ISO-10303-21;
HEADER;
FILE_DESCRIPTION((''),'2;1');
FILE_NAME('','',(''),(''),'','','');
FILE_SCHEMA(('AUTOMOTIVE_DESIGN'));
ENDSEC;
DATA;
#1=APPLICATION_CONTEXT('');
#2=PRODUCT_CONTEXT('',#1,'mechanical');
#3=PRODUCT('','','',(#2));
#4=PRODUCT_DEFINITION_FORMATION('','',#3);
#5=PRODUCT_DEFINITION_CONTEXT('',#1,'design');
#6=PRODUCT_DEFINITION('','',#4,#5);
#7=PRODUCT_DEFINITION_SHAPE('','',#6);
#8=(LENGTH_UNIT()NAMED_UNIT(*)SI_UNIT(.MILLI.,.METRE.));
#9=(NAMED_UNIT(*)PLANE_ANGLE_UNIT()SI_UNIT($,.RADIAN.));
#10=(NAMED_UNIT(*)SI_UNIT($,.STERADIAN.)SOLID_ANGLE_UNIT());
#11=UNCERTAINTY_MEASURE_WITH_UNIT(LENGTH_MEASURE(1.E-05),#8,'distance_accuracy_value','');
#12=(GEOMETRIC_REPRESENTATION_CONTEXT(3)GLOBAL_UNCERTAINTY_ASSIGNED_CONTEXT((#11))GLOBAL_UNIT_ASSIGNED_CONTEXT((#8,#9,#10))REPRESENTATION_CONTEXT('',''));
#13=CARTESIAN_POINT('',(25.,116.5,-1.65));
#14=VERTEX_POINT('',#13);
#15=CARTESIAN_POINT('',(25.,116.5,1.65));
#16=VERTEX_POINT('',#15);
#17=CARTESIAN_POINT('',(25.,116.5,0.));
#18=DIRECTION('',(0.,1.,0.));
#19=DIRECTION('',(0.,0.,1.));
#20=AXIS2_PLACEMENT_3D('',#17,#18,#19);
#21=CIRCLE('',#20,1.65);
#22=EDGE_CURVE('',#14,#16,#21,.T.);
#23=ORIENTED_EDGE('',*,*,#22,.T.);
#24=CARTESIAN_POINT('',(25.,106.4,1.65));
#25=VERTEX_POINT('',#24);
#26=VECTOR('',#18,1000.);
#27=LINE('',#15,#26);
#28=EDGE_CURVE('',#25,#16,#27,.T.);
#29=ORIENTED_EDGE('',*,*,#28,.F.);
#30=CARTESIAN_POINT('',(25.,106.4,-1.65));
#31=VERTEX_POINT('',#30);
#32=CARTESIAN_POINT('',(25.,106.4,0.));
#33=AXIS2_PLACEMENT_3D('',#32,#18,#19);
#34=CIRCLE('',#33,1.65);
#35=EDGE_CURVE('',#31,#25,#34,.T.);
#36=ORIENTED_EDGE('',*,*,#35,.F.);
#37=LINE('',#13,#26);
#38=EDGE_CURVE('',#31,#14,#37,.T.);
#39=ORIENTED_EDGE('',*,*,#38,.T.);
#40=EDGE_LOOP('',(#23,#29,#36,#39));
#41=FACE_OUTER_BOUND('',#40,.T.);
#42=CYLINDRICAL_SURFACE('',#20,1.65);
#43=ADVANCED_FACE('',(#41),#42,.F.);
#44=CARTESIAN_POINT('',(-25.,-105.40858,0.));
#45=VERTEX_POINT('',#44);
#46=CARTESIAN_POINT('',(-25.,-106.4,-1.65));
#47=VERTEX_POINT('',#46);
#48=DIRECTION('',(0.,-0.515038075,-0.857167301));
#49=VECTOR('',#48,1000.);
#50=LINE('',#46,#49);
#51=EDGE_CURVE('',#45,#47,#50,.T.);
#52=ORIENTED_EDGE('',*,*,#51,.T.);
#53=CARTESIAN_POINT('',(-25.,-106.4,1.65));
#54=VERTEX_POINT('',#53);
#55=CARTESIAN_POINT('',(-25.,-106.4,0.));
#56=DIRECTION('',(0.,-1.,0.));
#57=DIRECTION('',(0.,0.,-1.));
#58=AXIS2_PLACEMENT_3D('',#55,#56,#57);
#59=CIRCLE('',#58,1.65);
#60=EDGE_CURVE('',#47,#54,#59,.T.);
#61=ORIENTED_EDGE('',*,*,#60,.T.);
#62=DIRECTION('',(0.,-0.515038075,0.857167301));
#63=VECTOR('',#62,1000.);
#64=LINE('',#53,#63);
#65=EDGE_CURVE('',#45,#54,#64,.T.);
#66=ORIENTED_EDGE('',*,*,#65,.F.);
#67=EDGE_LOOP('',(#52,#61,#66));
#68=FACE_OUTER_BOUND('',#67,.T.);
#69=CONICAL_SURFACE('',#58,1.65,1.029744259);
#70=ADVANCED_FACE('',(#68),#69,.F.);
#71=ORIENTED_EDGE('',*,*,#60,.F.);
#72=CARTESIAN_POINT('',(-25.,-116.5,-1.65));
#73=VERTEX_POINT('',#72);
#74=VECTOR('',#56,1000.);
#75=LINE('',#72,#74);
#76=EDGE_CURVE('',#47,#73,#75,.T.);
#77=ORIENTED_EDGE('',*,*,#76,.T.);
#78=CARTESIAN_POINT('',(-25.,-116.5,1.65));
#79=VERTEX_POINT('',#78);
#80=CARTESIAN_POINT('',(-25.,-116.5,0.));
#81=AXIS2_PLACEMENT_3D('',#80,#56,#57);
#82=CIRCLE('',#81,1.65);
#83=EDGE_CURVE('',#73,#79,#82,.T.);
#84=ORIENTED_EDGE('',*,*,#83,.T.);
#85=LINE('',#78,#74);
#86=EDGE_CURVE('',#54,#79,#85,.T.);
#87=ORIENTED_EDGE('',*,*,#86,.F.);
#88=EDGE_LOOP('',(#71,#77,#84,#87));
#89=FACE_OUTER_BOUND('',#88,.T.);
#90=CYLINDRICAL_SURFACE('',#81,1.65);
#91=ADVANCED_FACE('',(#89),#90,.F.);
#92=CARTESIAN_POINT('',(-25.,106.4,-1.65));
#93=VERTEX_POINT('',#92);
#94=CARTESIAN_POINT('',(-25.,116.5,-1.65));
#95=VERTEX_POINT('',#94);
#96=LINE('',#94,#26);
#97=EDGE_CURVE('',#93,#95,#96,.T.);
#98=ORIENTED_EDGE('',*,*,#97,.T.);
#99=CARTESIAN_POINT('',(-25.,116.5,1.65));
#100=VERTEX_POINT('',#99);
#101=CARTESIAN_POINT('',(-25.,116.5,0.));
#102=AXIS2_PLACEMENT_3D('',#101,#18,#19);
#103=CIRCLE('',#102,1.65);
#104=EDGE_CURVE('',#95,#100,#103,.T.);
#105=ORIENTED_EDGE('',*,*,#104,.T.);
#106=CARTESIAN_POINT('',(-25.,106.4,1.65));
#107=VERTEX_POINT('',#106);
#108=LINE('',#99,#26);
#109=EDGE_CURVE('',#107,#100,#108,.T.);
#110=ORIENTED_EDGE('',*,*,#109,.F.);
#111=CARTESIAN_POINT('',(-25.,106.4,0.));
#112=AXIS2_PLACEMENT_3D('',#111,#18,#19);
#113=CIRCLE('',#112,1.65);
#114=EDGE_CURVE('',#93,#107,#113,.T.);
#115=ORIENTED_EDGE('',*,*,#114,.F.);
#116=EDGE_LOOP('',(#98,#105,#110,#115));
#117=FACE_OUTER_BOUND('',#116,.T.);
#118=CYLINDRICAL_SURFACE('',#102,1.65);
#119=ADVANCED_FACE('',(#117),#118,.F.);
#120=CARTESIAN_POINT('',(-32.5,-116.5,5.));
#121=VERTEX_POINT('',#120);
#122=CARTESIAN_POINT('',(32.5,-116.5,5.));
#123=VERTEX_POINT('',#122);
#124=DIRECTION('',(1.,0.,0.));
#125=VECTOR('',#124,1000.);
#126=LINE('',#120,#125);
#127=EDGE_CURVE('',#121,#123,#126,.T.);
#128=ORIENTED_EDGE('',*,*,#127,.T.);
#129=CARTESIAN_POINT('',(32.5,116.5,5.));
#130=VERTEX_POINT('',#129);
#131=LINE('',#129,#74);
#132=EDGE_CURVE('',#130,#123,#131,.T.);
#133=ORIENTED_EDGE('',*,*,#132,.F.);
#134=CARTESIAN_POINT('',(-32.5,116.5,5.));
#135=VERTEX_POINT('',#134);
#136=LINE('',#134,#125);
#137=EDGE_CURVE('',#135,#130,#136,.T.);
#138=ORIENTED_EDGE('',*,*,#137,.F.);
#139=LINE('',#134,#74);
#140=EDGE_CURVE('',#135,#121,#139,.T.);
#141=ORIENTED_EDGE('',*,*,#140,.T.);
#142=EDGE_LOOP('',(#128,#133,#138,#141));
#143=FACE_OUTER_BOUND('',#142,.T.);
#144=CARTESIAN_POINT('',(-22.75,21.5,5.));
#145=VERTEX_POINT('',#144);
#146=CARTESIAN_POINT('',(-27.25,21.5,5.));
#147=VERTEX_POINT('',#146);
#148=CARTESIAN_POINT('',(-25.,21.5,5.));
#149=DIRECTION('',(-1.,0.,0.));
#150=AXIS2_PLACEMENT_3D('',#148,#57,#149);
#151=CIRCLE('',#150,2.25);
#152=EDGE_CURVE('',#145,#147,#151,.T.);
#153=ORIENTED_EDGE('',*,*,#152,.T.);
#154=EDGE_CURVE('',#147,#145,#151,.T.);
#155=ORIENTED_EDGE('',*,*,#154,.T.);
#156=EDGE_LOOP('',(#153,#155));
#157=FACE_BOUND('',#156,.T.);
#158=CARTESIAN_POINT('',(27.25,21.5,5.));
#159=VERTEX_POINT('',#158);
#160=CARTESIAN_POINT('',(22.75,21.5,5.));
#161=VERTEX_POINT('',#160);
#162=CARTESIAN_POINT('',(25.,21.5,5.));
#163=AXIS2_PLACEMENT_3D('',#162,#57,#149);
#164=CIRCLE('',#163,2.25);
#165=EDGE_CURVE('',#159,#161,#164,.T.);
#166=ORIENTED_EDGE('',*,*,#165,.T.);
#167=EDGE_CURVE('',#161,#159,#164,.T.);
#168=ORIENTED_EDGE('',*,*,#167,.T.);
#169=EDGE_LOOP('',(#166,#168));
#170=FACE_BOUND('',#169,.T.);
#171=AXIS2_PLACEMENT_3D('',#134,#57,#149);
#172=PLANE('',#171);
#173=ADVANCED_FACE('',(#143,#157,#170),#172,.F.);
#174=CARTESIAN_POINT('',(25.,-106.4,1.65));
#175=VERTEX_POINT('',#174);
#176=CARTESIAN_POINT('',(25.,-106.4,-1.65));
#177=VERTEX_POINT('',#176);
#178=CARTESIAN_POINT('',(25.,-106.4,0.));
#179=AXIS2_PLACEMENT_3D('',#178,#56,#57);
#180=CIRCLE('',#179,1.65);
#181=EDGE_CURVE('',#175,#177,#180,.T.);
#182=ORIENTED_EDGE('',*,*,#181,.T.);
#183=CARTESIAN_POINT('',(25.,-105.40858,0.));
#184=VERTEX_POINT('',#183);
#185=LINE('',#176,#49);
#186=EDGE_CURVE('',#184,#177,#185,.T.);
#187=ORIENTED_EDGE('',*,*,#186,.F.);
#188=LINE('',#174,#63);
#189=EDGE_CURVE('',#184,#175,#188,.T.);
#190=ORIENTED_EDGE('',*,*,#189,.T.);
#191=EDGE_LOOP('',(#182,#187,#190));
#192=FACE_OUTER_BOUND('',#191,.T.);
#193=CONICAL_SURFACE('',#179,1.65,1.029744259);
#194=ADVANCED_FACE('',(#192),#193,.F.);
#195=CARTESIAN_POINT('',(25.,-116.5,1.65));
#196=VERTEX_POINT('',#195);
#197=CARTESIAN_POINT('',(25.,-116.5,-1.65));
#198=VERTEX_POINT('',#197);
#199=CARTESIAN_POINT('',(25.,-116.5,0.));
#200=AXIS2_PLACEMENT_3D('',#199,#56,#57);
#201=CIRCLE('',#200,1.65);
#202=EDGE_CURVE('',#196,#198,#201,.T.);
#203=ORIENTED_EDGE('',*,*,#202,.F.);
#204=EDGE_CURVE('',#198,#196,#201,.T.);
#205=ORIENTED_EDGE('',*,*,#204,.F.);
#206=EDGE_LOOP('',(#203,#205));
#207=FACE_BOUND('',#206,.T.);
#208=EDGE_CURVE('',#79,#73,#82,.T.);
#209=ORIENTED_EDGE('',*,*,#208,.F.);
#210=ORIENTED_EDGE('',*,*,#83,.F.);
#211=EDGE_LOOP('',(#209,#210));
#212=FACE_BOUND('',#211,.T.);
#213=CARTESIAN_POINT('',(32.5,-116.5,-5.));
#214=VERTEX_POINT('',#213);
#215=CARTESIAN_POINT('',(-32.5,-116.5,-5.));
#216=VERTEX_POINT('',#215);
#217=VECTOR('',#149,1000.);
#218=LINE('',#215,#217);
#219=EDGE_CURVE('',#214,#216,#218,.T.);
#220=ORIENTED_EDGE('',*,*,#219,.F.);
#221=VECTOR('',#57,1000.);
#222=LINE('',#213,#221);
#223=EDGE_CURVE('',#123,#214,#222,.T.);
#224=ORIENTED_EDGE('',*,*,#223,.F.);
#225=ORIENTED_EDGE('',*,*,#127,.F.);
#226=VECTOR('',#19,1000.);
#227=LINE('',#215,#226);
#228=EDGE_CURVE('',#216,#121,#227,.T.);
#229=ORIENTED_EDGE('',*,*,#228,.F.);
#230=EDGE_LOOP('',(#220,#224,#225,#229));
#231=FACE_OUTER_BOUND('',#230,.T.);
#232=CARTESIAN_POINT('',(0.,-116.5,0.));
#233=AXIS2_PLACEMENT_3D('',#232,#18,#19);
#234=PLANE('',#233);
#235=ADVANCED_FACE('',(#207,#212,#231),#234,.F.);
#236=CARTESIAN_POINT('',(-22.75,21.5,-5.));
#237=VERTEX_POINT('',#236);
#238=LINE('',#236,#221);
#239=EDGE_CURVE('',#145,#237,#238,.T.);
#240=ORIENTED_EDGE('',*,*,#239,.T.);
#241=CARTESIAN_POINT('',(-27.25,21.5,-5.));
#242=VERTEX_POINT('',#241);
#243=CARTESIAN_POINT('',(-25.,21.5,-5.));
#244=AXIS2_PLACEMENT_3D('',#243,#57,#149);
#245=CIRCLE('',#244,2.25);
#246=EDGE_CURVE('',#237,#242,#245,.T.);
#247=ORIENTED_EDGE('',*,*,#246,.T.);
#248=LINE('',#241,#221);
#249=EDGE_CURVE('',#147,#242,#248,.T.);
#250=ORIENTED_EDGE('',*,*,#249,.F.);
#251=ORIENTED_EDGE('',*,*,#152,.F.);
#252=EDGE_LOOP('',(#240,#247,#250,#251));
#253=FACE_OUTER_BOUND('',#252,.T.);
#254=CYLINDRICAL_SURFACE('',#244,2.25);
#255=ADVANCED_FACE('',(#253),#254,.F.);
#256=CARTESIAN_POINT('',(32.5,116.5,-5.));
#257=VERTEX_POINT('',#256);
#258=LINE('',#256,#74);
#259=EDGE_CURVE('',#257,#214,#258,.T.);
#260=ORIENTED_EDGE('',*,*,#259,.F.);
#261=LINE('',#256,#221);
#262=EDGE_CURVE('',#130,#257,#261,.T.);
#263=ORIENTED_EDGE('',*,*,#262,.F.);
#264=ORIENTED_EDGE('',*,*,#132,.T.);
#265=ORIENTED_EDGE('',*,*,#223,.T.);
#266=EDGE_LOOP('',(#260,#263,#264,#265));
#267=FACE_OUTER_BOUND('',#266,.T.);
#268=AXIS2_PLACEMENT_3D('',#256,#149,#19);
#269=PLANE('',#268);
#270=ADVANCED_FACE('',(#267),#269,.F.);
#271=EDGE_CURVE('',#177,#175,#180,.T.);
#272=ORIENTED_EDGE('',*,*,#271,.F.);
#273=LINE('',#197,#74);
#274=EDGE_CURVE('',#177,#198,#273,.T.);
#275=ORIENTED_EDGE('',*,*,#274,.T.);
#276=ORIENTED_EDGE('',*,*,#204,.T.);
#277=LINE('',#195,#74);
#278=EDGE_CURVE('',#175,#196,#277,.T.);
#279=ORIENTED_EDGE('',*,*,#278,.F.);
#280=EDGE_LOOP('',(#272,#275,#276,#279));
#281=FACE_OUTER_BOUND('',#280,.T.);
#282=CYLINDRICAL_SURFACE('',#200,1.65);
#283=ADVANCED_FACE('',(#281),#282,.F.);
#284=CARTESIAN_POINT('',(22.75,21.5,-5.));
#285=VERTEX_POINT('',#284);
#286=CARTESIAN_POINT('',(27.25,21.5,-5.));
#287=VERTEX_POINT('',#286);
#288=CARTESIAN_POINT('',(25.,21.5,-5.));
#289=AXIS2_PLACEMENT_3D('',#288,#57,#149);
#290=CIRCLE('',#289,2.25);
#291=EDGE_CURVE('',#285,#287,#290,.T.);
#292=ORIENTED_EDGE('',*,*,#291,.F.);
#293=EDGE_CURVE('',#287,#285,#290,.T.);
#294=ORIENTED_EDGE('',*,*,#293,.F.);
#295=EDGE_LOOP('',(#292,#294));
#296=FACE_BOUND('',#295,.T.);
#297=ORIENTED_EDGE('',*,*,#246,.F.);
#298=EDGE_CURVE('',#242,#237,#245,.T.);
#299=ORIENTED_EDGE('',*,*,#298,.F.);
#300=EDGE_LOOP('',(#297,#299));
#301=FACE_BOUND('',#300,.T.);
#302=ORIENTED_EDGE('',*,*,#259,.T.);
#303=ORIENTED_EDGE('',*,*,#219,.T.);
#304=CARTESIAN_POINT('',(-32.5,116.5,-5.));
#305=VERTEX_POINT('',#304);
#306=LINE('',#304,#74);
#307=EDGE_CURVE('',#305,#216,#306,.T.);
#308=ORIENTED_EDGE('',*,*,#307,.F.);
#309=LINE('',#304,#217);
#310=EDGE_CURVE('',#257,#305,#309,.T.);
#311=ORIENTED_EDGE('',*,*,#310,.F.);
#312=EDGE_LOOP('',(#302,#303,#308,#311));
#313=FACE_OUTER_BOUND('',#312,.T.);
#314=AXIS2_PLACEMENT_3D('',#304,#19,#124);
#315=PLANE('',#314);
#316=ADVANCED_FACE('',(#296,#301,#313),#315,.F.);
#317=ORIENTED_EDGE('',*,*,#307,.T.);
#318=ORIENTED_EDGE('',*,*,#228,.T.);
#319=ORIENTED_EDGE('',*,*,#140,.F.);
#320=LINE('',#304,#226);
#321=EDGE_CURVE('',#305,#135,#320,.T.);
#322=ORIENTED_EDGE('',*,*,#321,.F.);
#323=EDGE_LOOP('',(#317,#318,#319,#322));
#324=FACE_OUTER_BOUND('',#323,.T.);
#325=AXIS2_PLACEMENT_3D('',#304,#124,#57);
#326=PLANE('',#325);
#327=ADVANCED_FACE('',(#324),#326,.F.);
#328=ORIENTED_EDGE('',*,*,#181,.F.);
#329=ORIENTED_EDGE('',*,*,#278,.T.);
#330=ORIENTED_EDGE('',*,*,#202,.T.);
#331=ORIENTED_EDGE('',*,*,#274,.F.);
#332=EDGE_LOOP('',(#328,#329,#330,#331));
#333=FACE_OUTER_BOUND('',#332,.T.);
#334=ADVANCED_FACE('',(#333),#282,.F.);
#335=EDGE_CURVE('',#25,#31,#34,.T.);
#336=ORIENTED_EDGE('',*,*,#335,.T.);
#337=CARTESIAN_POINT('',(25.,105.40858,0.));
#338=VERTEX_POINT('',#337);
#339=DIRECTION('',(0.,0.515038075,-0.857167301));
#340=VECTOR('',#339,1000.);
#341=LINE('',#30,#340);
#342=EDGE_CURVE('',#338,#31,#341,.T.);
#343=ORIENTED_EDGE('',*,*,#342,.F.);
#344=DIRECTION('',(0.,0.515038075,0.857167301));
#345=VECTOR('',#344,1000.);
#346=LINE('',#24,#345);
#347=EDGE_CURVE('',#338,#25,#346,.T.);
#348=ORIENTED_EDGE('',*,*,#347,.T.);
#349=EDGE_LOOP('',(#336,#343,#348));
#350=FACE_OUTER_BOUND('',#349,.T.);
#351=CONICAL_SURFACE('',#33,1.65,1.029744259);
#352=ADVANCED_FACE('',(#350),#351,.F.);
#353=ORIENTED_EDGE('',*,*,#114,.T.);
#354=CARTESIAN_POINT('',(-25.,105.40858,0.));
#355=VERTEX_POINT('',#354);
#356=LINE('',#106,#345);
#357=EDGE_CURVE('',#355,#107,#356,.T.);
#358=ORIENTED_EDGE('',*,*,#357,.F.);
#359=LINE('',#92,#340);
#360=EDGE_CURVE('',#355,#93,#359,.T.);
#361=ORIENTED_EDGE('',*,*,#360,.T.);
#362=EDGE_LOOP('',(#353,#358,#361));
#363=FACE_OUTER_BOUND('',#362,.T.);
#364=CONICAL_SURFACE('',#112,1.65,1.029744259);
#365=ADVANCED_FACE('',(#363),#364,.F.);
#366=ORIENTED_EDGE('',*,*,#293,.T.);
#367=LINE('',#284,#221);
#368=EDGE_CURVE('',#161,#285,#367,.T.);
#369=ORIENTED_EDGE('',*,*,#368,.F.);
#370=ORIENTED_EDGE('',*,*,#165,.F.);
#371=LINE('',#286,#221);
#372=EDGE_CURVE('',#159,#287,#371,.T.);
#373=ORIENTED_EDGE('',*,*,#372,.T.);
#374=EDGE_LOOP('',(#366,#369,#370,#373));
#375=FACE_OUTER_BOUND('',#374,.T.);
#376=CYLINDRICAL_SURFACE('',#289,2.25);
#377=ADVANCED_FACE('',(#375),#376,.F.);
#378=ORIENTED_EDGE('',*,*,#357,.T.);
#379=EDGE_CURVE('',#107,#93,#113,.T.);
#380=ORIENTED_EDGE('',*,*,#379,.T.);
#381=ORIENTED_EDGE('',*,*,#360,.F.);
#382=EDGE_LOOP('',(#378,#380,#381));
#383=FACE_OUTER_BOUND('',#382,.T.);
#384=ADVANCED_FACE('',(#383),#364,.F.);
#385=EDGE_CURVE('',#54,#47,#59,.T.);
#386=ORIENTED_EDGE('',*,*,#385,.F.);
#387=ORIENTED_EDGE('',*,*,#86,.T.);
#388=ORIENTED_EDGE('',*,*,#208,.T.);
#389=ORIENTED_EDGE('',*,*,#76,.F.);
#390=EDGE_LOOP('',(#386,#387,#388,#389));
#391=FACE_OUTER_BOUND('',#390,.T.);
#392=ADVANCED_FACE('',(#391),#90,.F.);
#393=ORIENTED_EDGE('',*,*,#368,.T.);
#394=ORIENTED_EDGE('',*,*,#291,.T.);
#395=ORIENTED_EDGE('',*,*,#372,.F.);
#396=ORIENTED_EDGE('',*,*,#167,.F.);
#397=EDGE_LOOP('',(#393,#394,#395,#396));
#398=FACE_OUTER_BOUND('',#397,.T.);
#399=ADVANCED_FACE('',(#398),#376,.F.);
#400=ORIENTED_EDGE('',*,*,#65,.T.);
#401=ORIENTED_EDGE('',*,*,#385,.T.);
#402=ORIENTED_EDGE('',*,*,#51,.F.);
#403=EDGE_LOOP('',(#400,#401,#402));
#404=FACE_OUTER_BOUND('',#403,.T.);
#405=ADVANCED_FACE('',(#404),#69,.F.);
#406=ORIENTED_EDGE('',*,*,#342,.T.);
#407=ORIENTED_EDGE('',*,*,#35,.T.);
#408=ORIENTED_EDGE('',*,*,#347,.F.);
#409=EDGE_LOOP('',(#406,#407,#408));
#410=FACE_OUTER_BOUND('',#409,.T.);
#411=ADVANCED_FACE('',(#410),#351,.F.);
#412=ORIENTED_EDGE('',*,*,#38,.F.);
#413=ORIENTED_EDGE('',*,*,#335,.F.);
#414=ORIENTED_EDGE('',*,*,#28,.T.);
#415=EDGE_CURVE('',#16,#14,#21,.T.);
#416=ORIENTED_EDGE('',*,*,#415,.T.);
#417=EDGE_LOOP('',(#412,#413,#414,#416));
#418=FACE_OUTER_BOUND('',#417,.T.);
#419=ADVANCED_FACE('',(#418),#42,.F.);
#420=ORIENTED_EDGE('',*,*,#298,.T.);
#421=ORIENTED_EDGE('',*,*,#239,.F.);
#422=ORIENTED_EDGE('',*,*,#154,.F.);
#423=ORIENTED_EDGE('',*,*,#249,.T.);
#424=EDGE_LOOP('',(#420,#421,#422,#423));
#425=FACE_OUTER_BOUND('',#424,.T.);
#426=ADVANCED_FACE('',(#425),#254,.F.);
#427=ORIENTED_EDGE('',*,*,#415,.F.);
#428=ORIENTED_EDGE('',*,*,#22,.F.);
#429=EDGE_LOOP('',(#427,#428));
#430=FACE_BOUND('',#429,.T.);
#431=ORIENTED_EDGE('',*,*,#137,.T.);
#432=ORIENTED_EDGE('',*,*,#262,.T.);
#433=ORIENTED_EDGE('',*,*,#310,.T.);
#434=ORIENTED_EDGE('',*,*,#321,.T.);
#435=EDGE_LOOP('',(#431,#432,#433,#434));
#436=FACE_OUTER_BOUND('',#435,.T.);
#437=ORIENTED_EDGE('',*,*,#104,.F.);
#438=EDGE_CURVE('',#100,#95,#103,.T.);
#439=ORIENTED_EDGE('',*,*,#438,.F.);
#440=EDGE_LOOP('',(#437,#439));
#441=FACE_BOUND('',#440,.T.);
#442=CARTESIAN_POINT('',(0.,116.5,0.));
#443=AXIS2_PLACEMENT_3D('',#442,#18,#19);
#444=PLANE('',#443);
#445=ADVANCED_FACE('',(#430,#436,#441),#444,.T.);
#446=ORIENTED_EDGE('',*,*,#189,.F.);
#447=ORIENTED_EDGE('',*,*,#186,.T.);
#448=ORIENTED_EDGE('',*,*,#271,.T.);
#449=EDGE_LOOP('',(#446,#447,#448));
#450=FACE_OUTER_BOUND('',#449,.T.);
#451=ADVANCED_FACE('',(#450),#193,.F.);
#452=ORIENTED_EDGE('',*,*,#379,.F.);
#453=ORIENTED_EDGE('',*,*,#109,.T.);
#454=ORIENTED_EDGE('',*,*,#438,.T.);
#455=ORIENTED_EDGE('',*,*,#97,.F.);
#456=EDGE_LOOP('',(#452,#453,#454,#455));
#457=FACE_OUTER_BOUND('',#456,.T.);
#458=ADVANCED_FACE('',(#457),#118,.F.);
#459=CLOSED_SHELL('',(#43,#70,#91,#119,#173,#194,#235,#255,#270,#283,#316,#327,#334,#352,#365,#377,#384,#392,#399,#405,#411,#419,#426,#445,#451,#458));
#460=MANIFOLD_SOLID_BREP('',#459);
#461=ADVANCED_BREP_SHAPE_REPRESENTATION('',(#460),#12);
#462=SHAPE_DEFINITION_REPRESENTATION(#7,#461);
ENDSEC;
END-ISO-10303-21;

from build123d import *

# Parameters (mm, degrees)
SKETCH_1_W                  = 65
SKETCH_1_H                  = 10
EXTRUDE_1_DEPTH             = 116.5
HOLE_WIZARD_M4_1_AT_2_COUNT = 2
HOLE_WIZARD_M4_1_AT_2_PITCH = 50
HOLE_WIZARD_M4_1_2_D        = 4.5


with BuildPart() as part:
    # 草图1 → 凸台-拉伸1 (new, symmetric)
    with BuildSketch(Plane(origin=(0, 0, 0), x_dir=(1, 0, 0), z_dir=(0, 1, 0))):
        Rectangle(SKETCH_1_W, SKETCH_1_H)
    extrude(amount=EXTRUDE_1_DEPTH, both=True)

    # 草图3 → Hole Wizard M4 _1 (revolve, cut)
    with BuildSketch(Plane(origin=(25, 116.5, 0), x_dir=(0, 0, 1), z_dir=(1, 0, 0))):
        Polygon((0, 0), (0, 11.091420021), (1.65, 10.1), (1.65, 0), align=None)
    hole_wizard_m4_1 = revolve(axis=Axis((25, 122.85, 0), (0, -1, 0)), mode=Mode.SUBTRACT)

    # Hole Wizard M4 _1 at 2: Hole Wizard M4 _1 ×2
    with Locations(*[(-i * HOLE_WIZARD_M4_1_AT_2_PITCH, 0, 0) for i in range(1, HOLE_WIZARD_M4_1_AT_2_COUNT)]):
        add(hole_wizard_m4_1, mode=Mode.SUBTRACT)

    # 镜向1: Hole Wizard M4 _1 across plane
    add(hole_wizard_m4_1.mirror(Plane.ZX), mode=Mode.SUBTRACT)

    # 镜向1 copy 1 sketch → 镜向1 copy 1 (revolve, cut)
    with BuildSketch(Plane(origin=(-25, -116.5, 0), x_dir=(0, 0, 1), z_dir=(1, 0, 0))):
        Polygon((0, 0), (0, -11.091420021), (1.65, -10.1), (1.65, 0), align=None)
    revolve(axis=Axis((-25, -122.85, 0), (0, -1, 0)), mode=Mode.SUBTRACT)

    # Hole Wizard M4 _1 2 (through all)
    with Locations(Plane(origin=(0, 0, -5), x_dir=(-1, 0, 0), z_dir=(0, 0, -1))):
        with Locations((25, 21.5), (-25, 21.5)):
            Hole(HOLE_WIZARD_M4_1_2_D / 2)


solid = part.part
